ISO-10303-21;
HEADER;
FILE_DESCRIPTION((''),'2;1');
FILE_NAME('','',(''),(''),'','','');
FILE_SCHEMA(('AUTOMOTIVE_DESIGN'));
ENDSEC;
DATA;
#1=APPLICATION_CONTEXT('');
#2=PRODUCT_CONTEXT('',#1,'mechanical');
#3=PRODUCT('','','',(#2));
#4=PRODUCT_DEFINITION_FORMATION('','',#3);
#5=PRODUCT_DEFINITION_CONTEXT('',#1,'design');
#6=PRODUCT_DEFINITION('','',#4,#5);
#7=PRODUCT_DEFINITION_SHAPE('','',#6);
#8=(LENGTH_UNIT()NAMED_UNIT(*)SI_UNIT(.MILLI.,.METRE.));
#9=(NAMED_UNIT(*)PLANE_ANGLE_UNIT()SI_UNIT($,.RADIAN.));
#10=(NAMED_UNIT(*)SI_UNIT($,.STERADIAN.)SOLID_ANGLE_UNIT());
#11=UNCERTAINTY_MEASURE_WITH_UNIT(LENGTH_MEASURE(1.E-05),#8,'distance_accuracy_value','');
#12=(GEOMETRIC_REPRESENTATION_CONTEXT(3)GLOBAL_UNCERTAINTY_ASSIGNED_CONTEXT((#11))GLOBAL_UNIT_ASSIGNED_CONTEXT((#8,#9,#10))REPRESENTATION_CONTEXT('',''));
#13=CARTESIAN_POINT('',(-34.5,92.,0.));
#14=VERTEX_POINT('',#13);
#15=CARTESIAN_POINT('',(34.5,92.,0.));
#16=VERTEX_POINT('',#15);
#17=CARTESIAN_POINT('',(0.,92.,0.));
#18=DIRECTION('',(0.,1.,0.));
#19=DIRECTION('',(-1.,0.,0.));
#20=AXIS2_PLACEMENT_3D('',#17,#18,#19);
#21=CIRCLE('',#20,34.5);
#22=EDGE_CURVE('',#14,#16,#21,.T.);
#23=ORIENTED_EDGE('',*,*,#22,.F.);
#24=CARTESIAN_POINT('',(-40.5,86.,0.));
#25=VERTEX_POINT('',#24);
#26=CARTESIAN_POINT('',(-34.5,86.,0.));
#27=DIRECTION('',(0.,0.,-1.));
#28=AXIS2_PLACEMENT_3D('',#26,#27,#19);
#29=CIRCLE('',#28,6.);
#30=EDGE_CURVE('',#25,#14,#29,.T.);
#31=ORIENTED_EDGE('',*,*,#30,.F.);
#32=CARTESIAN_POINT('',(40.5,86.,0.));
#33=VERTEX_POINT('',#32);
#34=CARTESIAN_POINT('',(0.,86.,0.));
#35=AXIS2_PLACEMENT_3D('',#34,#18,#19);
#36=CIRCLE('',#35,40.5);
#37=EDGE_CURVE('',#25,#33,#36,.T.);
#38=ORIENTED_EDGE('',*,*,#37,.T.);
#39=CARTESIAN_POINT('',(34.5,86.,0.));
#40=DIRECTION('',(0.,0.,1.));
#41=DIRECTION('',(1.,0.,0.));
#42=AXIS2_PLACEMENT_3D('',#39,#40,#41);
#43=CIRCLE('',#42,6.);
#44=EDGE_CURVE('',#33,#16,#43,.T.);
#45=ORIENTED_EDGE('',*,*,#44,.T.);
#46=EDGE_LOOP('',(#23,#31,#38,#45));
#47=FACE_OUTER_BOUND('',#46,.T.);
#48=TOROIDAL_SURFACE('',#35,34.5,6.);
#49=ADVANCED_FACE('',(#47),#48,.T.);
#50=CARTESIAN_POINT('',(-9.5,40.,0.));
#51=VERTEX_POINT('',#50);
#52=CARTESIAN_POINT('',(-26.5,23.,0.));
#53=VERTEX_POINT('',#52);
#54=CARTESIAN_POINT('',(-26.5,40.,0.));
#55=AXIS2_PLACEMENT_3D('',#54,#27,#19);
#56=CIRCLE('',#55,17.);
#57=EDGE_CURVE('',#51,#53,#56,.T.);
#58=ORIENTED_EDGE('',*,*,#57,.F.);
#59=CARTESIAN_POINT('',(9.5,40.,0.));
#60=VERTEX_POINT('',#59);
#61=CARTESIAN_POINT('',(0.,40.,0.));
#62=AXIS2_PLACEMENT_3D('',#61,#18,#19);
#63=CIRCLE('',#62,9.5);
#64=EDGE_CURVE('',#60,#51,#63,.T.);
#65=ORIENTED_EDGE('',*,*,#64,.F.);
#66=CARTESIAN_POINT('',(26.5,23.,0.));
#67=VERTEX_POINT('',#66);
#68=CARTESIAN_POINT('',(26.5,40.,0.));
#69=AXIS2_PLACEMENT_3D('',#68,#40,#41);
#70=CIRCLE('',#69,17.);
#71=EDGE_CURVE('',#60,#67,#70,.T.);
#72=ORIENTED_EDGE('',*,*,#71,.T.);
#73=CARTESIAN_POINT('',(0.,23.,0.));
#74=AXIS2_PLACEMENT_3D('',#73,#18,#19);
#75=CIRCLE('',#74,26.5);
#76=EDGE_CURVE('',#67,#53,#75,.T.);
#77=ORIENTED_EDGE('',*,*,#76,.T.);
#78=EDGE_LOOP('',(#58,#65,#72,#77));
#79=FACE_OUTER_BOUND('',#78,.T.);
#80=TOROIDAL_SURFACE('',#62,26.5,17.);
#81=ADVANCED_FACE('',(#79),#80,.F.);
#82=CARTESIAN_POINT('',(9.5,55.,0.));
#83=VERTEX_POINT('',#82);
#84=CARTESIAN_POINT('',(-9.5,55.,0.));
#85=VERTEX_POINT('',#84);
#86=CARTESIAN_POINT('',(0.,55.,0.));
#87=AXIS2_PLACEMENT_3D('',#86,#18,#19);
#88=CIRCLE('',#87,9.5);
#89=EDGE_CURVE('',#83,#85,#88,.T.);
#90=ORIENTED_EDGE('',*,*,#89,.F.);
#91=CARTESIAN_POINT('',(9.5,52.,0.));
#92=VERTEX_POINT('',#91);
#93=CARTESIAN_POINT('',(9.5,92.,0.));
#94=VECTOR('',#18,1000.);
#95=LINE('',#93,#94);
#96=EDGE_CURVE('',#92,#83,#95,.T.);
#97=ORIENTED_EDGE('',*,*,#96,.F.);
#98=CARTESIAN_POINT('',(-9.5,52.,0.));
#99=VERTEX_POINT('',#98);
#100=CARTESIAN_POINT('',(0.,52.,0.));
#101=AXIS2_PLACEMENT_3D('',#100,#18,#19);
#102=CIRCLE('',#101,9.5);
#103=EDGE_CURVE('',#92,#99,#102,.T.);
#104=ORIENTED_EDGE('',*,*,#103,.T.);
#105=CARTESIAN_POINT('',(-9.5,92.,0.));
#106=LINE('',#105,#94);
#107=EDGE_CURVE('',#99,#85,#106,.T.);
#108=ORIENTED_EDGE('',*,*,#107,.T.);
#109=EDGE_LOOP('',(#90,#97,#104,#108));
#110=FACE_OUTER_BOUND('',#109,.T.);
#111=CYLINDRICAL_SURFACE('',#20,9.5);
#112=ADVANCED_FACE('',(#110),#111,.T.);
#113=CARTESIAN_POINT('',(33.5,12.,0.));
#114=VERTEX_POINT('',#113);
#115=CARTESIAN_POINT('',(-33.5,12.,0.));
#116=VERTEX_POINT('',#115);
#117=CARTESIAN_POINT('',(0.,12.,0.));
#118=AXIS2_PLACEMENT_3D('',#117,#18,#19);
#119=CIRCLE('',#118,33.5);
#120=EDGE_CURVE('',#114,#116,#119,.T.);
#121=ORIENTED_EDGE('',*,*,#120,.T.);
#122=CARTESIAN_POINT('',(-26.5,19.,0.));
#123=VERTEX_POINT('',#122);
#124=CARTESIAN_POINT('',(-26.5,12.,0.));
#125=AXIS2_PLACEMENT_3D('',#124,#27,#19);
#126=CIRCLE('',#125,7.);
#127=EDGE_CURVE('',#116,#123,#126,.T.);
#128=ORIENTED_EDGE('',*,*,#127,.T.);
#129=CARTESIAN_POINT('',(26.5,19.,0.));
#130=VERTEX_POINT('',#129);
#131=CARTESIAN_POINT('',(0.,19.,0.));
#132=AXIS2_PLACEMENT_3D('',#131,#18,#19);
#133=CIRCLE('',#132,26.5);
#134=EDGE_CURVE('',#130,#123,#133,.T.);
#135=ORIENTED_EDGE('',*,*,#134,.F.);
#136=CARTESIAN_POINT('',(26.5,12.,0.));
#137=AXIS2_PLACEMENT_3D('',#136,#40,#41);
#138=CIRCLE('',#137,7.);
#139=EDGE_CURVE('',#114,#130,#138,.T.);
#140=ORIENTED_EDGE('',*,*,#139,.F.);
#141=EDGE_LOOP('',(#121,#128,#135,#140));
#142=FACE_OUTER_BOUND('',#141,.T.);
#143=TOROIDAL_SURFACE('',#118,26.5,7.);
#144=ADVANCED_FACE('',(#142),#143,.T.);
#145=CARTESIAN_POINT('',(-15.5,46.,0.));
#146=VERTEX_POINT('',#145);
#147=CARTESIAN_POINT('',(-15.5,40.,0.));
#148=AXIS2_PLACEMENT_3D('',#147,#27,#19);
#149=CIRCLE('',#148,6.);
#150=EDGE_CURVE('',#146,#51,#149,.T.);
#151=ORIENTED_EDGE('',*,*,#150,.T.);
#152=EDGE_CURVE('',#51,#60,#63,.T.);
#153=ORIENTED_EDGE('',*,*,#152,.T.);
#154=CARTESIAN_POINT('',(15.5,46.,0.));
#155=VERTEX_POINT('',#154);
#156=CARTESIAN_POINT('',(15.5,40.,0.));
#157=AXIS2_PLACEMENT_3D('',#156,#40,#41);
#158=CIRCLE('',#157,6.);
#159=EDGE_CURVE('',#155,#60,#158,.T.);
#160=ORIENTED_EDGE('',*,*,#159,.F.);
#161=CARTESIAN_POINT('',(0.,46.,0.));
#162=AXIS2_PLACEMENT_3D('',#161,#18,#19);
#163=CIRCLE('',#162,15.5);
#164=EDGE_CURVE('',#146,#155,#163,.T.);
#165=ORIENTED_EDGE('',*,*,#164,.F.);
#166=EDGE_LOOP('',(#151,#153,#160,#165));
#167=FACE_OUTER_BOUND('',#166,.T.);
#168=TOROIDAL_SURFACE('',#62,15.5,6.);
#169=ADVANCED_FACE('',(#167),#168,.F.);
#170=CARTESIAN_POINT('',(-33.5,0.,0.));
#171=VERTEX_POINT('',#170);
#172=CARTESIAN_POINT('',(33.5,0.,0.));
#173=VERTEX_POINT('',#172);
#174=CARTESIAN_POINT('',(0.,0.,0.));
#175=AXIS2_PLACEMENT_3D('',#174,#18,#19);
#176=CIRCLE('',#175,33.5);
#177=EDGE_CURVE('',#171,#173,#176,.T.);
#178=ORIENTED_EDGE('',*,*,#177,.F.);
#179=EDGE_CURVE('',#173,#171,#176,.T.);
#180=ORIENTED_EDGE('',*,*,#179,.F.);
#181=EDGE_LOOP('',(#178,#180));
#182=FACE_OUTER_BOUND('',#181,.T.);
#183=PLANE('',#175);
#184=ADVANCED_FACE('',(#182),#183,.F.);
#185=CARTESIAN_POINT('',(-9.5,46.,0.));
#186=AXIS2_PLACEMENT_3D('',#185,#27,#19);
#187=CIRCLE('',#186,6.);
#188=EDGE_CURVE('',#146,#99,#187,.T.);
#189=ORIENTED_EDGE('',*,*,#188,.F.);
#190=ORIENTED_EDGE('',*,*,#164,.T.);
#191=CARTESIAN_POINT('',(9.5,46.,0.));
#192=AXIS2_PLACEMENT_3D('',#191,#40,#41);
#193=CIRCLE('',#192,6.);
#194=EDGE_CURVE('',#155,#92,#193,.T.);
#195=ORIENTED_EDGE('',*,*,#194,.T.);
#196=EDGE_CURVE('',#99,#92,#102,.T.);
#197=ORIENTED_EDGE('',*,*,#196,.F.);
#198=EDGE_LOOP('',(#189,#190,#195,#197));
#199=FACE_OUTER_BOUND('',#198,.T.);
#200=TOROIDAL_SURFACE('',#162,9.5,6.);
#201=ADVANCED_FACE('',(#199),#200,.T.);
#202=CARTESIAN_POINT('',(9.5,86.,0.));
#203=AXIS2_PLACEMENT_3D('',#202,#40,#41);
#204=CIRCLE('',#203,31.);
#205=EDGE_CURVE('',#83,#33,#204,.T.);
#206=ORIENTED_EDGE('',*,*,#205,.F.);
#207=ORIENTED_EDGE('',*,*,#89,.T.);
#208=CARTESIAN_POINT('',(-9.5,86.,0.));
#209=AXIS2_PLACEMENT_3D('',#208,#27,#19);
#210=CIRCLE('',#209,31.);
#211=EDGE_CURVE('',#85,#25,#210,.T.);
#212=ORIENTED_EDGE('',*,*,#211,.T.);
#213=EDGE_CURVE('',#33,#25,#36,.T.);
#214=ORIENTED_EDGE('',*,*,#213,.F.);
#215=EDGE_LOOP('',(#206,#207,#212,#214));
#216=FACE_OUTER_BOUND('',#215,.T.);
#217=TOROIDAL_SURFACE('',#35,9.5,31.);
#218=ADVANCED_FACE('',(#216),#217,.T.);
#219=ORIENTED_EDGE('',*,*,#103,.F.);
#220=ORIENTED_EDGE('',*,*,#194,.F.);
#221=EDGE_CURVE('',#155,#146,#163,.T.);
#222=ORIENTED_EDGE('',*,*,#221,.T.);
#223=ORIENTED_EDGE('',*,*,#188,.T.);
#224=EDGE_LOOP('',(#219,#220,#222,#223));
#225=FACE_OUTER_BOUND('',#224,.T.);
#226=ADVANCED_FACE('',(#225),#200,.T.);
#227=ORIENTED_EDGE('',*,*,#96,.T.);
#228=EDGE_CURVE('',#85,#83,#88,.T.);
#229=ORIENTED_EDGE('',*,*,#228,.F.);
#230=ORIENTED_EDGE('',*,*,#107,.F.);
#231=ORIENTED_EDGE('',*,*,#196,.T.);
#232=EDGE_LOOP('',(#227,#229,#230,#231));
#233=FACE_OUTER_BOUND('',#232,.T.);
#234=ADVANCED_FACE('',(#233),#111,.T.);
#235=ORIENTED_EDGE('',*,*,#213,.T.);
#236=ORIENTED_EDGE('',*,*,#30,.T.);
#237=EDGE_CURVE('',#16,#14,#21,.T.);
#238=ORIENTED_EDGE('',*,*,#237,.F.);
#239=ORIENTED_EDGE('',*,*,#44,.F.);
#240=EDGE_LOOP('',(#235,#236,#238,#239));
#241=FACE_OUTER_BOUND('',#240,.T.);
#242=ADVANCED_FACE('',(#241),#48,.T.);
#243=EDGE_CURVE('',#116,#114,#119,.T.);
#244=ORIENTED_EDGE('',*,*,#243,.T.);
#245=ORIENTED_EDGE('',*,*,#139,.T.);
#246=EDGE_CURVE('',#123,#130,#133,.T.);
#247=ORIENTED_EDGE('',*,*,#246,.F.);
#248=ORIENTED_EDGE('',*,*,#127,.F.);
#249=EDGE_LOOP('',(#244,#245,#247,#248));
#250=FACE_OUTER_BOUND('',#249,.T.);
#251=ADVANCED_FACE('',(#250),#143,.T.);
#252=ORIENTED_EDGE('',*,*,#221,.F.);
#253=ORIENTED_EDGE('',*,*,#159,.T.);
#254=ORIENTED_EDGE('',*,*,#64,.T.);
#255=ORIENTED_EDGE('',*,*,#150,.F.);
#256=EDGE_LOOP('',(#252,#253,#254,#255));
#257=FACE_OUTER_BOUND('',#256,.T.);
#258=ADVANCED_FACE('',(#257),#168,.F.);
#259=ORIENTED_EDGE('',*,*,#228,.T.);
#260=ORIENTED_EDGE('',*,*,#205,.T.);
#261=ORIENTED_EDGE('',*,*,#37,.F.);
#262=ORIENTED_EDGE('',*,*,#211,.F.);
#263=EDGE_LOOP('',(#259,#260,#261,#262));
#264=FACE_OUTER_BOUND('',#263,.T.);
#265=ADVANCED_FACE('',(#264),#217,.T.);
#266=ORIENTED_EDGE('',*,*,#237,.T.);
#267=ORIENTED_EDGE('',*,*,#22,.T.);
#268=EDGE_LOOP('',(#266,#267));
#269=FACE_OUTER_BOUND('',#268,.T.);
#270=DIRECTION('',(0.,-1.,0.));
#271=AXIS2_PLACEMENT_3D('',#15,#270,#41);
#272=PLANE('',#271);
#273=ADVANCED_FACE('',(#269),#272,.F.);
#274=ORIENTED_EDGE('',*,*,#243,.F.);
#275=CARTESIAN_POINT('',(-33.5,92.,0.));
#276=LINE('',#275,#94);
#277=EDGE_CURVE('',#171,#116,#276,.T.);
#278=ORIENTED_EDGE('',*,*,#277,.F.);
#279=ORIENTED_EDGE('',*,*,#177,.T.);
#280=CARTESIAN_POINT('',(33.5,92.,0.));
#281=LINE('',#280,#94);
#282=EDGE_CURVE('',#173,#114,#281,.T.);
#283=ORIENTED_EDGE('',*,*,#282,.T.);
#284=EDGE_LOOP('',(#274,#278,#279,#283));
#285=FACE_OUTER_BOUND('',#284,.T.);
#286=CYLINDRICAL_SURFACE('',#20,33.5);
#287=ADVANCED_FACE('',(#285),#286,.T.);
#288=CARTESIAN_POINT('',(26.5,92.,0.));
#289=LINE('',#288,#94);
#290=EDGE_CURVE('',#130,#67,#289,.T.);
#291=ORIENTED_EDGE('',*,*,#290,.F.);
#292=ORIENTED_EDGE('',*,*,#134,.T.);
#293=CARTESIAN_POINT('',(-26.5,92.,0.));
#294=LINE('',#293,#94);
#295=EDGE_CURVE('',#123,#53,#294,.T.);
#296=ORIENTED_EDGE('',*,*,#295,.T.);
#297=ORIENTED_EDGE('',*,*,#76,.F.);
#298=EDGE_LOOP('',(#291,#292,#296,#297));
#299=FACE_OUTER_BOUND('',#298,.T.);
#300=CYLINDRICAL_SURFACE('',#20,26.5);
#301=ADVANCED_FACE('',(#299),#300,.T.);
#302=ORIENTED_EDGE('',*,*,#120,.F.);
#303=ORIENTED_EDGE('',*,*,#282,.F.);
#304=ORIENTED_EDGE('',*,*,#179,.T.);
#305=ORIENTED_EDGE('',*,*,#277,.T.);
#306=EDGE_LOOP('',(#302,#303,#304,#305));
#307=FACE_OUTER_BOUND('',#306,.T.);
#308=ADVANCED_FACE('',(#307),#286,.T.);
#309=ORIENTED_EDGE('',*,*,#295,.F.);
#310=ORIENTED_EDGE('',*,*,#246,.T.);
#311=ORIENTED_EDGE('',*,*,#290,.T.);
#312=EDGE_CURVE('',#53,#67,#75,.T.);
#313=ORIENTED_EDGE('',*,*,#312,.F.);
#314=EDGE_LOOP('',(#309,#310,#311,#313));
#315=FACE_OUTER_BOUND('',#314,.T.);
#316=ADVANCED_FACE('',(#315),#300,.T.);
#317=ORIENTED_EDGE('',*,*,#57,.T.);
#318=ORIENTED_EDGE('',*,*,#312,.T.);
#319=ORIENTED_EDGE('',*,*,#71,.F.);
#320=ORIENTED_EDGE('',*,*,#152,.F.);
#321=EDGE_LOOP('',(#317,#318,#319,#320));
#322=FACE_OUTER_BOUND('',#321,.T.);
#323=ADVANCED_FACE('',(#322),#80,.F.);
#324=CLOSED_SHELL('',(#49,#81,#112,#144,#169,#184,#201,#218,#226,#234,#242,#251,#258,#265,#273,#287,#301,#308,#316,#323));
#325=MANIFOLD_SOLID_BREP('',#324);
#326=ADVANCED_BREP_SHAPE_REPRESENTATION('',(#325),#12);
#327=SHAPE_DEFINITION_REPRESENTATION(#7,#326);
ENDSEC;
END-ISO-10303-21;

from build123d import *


with BuildPart() as part:
    # Knob Profile Sketch → Knob Body Revolve (revolve)
    with BuildSketch(Plane.XY, mode=Mode.PRIVATE) as knob_body_revolve_sk:
        with BuildLine():
            Line((0, 0), (33.5, 0))
            Line((33.5, 0), (33.5, 12))
            ThreePointArc((33.5, 12), (31.449747468, 16.949747468), (26.5, 19))
            Line((26.5, 19), (26.5, 23))
            ThreePointArc((26.5, 23), (14.47918472, 27.97918472), (9.5, 40))
            ThreePointArc((9.5, 40), (11.257359313, 44.242640687), (15.5, 46))
            ThreePointArc((15.5, 46), (13.742640687, 50.242640687), (9.5, 52))
            Line((9.5, 52), (9.5, 55))
            ThreePointArc((9.5, 55), (31.420310217, 64.079689783), (40.5, 86))
            ThreePointArc((40.5, 86), (38.742640687, 90.242640687), (34.5, 92))
            Line((34.5, 92), (0, 92))
            Line((0, 92), (0, 0))
        make_face()
    revolve(knob_body_revolve_sk.sketch.rotate(Axis((0, 92, 0), (0, -1, 0)), 180), axis=Axis((0, 92, 0), (0, -1, 0)))


solid = part.part
